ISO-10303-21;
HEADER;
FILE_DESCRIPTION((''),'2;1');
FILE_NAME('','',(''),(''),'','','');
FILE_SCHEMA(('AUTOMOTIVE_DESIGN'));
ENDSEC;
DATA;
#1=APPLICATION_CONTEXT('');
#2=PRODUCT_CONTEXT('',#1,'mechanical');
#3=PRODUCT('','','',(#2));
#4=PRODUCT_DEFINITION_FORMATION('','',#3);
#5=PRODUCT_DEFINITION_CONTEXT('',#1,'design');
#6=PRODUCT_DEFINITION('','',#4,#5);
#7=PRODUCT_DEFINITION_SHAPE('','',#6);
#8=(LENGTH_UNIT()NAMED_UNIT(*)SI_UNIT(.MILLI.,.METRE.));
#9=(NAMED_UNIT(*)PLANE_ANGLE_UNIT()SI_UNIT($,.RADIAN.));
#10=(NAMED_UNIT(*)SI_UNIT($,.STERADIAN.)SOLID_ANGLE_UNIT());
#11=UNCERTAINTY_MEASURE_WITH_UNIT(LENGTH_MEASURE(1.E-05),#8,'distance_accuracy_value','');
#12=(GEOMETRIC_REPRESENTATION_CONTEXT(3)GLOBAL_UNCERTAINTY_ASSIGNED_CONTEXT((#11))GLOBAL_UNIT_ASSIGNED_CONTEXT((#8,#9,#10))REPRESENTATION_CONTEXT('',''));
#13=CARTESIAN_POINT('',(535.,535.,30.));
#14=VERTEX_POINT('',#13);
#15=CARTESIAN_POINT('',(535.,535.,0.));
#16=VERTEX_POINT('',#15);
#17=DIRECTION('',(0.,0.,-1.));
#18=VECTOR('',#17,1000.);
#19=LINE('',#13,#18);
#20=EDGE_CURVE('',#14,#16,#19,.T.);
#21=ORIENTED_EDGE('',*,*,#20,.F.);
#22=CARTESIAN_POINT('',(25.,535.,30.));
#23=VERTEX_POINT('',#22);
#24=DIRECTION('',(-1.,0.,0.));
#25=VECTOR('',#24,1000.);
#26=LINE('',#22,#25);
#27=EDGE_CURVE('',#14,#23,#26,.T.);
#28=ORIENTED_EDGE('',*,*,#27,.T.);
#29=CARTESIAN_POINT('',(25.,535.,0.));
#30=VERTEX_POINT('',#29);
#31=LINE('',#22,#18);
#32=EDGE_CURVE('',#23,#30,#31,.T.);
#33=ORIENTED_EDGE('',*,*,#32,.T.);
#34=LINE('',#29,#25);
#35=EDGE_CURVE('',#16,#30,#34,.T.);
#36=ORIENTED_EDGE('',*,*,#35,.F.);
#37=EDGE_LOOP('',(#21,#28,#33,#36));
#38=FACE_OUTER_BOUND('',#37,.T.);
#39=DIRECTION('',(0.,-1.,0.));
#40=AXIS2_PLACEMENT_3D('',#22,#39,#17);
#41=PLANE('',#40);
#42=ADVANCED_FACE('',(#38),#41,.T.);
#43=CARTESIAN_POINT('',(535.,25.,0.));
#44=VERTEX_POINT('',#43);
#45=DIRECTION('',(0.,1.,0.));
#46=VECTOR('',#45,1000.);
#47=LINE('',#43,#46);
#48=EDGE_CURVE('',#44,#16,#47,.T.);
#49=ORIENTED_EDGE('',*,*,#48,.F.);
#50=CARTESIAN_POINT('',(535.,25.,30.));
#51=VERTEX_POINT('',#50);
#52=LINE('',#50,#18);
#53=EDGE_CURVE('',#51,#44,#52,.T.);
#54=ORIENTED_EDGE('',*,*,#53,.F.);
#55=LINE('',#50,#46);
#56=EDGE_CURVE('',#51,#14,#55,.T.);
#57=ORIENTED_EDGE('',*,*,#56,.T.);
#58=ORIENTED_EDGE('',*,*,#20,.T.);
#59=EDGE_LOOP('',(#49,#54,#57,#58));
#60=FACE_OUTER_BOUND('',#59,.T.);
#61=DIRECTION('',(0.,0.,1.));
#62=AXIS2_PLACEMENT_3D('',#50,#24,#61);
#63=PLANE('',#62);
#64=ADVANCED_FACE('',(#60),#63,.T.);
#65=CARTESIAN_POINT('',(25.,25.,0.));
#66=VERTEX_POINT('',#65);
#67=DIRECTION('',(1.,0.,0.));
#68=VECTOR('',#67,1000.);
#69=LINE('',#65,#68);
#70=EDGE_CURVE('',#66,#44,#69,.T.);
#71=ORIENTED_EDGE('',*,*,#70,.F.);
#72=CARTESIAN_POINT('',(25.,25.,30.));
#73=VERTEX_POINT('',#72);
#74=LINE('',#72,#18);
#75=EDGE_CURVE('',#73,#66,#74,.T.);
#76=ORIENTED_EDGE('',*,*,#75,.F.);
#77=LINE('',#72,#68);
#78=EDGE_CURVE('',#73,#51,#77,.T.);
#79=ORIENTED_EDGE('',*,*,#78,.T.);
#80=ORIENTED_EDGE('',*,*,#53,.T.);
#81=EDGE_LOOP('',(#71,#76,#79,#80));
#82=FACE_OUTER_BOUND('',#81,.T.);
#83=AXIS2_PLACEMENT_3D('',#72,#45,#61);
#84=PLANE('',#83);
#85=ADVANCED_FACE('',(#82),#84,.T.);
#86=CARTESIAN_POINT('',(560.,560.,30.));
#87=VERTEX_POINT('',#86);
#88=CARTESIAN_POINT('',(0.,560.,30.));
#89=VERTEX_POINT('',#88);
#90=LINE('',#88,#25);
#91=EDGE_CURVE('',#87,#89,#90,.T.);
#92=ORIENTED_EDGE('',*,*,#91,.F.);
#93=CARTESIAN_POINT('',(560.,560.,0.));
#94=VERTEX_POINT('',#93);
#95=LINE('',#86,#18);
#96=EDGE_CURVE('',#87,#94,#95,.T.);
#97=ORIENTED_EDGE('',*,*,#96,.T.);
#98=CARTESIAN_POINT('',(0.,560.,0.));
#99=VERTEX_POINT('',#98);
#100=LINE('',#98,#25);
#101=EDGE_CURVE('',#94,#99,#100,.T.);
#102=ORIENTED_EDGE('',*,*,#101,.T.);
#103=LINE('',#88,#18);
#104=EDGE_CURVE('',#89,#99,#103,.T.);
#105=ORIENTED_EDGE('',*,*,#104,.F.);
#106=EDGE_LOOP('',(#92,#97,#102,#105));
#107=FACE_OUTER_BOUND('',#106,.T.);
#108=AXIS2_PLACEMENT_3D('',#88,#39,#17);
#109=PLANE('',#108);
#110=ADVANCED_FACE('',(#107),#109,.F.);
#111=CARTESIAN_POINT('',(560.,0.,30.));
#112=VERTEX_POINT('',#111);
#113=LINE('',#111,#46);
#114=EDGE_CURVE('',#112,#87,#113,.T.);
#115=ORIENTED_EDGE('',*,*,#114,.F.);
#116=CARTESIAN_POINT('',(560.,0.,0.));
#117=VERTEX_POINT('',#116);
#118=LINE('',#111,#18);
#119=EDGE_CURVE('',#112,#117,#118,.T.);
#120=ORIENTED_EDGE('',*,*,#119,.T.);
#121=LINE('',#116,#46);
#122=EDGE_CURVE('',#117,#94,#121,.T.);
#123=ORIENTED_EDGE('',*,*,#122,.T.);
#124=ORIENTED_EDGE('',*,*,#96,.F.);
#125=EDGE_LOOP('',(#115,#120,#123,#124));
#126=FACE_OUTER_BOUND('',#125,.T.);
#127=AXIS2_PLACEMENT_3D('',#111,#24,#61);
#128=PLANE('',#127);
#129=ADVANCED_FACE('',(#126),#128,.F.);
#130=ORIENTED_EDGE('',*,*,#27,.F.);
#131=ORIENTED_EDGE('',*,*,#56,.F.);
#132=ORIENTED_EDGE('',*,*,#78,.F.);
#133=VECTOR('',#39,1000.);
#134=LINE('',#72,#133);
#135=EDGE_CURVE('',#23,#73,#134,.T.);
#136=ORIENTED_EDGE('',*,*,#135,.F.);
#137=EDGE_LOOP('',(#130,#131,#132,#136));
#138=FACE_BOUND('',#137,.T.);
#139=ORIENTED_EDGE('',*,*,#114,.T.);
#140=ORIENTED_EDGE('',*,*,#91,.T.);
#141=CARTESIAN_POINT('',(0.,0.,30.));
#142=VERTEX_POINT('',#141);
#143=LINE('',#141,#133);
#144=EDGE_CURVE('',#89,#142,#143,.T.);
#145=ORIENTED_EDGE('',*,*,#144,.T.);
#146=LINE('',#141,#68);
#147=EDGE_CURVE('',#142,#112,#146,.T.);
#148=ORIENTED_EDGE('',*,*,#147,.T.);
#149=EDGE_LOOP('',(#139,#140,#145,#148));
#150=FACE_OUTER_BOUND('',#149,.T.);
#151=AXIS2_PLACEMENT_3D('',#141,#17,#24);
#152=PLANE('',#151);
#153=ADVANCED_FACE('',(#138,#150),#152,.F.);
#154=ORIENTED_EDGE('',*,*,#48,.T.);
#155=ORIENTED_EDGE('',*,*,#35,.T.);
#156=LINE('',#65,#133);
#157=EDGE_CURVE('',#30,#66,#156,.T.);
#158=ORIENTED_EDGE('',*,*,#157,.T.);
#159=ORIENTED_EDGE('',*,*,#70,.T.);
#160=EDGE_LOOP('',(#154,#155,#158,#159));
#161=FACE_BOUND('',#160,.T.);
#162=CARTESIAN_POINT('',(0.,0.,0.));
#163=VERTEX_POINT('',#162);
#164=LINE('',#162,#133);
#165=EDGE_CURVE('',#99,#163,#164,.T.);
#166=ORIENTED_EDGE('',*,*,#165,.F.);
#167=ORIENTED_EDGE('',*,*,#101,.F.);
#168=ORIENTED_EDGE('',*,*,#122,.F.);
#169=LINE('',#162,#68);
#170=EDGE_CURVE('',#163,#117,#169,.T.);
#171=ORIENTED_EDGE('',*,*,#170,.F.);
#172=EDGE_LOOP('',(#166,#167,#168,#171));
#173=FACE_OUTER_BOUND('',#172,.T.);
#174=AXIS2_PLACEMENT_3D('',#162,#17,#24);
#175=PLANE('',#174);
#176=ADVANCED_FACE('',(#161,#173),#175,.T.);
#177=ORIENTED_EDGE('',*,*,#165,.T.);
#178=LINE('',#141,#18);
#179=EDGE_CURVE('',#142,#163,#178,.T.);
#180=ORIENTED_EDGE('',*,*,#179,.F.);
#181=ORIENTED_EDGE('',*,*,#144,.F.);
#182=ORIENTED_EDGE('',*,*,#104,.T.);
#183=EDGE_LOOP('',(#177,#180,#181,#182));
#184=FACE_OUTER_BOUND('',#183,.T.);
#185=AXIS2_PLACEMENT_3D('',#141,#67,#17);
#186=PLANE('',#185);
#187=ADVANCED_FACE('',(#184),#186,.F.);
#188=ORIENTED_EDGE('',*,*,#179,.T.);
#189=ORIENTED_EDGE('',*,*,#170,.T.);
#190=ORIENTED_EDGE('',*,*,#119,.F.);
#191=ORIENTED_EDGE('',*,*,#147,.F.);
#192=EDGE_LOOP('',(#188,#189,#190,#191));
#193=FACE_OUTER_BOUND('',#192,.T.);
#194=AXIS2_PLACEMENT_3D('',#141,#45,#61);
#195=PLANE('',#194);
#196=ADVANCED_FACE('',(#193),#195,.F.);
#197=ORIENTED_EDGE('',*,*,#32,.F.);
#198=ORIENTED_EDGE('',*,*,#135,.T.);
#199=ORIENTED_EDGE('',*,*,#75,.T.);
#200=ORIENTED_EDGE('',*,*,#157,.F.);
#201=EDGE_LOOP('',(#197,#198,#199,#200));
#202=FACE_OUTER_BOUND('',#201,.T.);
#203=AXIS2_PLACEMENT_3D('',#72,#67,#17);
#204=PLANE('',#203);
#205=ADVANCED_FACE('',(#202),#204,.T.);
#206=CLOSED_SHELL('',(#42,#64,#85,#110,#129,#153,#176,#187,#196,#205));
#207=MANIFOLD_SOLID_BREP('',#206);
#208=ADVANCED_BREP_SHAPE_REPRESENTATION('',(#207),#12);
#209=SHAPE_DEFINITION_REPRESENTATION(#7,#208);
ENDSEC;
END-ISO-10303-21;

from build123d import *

# Parameters (mm, degrees)
SKETCH1_W           = 560
SKETCH1_H           = 560
SKETCH1_W_2         = 510
SKETCH1_H_2         = 510
BOSS_EXTRUDE1_DEPTH = 30


with BuildPart() as part:
    # Sketch1 → Boss-Extrude1 (new body)
    with BuildSketch(Plane.XY):
        with Locations((280, 280)):
            Rectangle(SKETCH1_W, SKETCH1_H)
        with Locations((280, 280)):
            Rectangle(SKETCH1_W_2, SKETCH1_H_2, mode=Mode.SUBTRACT)
    extrude(amount=BOSS_EXTRUDE1_DEPTH)


solid = part.part
